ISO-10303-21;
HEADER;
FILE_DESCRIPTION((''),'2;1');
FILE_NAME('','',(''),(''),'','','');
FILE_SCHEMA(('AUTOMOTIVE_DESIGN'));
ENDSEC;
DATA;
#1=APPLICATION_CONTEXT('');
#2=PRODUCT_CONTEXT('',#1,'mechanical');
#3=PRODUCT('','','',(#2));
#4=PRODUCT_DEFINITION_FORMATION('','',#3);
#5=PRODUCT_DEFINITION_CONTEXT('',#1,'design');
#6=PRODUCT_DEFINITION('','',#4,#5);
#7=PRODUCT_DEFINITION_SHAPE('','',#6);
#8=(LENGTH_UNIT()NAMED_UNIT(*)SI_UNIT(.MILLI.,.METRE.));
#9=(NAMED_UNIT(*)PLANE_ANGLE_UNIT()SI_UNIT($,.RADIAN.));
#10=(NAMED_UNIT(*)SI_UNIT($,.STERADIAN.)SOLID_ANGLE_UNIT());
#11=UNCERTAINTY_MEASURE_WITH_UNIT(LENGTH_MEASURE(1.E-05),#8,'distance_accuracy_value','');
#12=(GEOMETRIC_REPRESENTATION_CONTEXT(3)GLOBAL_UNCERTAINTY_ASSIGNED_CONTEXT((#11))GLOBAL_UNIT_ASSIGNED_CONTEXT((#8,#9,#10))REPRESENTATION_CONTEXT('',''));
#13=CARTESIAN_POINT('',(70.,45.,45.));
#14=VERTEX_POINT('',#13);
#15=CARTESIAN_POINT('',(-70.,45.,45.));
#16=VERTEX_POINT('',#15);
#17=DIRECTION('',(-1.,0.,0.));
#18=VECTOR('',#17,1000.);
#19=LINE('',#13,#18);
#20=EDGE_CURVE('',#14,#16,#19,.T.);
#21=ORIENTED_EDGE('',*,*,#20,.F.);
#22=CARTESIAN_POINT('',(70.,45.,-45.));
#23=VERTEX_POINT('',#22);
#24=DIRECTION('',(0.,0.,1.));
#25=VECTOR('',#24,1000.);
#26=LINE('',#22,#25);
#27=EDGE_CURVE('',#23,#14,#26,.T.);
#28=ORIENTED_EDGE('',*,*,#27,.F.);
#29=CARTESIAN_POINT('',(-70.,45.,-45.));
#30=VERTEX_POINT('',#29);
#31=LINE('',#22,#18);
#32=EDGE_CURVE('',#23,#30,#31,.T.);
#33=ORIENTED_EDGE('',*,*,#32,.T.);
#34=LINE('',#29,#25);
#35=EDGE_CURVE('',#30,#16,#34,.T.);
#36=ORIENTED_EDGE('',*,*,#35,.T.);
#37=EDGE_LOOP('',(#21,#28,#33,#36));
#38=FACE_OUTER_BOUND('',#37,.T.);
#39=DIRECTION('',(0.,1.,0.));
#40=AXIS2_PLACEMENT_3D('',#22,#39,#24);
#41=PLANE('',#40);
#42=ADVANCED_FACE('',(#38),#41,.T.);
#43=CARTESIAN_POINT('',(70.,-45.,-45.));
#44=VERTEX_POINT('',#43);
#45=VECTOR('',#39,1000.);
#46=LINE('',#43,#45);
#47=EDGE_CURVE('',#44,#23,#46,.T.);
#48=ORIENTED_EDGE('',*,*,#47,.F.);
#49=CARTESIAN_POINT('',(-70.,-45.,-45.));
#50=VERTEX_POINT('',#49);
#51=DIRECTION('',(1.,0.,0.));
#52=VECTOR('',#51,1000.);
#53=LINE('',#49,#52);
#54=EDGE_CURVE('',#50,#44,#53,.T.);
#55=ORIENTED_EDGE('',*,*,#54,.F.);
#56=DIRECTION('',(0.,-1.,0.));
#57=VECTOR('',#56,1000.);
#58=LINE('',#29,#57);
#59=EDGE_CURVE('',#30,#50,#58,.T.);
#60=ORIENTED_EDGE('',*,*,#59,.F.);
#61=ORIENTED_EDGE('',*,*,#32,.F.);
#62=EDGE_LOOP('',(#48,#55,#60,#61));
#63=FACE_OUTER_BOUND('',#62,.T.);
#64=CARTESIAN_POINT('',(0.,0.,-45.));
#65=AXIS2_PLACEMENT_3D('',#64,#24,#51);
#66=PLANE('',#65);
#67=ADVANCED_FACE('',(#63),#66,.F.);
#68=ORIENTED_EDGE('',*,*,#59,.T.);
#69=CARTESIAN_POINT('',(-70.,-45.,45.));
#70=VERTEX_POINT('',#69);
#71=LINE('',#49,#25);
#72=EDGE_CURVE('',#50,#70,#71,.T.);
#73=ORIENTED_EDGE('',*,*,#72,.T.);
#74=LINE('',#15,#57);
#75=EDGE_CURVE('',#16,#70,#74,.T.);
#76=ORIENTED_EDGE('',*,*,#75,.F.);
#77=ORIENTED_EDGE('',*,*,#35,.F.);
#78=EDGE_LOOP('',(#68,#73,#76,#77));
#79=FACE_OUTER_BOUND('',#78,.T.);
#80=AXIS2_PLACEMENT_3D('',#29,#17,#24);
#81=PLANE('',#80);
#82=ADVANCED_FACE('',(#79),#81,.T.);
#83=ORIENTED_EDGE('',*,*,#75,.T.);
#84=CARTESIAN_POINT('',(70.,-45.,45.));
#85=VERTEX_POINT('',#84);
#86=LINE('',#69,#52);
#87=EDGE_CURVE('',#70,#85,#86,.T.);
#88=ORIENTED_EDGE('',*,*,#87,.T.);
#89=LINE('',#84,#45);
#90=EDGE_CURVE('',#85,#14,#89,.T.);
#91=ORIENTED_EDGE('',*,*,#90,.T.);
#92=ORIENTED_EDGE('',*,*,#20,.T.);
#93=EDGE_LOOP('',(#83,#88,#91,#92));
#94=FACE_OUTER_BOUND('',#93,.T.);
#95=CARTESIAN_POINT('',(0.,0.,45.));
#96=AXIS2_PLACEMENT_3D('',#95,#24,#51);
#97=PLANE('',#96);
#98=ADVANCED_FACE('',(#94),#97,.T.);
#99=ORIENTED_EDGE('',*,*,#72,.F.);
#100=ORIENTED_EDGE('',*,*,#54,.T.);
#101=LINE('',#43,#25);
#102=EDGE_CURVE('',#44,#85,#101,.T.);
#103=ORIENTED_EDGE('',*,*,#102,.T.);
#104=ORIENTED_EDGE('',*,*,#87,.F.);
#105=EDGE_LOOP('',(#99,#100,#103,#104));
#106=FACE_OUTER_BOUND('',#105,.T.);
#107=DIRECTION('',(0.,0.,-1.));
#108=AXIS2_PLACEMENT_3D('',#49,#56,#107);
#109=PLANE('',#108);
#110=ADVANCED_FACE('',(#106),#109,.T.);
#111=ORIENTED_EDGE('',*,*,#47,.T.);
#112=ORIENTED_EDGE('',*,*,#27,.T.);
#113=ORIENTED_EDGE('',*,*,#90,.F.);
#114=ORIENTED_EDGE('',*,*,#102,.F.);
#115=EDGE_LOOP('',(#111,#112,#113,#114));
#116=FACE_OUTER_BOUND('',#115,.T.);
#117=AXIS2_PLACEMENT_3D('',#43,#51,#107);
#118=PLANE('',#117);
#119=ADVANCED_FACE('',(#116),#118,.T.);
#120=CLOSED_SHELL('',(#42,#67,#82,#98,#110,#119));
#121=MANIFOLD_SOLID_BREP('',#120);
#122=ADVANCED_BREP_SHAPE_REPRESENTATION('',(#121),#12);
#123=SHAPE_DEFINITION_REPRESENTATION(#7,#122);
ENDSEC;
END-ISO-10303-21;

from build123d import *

# Parameters (mm, degrees)
SKETCH_1_W      = 140
SKETCH_1_H      = 90
EXTRUDE_1_DEPTH = 45


with BuildPart() as part:
    # 草图1 → 凸台-拉伸1 (new, symmetric)
    with BuildSketch(Plane.XY):
        Rectangle(SKETCH_1_W, SKETCH_1_H)
    extrude(amount=EXTRUDE_1_DEPTH, both=True)


solid = part.part
